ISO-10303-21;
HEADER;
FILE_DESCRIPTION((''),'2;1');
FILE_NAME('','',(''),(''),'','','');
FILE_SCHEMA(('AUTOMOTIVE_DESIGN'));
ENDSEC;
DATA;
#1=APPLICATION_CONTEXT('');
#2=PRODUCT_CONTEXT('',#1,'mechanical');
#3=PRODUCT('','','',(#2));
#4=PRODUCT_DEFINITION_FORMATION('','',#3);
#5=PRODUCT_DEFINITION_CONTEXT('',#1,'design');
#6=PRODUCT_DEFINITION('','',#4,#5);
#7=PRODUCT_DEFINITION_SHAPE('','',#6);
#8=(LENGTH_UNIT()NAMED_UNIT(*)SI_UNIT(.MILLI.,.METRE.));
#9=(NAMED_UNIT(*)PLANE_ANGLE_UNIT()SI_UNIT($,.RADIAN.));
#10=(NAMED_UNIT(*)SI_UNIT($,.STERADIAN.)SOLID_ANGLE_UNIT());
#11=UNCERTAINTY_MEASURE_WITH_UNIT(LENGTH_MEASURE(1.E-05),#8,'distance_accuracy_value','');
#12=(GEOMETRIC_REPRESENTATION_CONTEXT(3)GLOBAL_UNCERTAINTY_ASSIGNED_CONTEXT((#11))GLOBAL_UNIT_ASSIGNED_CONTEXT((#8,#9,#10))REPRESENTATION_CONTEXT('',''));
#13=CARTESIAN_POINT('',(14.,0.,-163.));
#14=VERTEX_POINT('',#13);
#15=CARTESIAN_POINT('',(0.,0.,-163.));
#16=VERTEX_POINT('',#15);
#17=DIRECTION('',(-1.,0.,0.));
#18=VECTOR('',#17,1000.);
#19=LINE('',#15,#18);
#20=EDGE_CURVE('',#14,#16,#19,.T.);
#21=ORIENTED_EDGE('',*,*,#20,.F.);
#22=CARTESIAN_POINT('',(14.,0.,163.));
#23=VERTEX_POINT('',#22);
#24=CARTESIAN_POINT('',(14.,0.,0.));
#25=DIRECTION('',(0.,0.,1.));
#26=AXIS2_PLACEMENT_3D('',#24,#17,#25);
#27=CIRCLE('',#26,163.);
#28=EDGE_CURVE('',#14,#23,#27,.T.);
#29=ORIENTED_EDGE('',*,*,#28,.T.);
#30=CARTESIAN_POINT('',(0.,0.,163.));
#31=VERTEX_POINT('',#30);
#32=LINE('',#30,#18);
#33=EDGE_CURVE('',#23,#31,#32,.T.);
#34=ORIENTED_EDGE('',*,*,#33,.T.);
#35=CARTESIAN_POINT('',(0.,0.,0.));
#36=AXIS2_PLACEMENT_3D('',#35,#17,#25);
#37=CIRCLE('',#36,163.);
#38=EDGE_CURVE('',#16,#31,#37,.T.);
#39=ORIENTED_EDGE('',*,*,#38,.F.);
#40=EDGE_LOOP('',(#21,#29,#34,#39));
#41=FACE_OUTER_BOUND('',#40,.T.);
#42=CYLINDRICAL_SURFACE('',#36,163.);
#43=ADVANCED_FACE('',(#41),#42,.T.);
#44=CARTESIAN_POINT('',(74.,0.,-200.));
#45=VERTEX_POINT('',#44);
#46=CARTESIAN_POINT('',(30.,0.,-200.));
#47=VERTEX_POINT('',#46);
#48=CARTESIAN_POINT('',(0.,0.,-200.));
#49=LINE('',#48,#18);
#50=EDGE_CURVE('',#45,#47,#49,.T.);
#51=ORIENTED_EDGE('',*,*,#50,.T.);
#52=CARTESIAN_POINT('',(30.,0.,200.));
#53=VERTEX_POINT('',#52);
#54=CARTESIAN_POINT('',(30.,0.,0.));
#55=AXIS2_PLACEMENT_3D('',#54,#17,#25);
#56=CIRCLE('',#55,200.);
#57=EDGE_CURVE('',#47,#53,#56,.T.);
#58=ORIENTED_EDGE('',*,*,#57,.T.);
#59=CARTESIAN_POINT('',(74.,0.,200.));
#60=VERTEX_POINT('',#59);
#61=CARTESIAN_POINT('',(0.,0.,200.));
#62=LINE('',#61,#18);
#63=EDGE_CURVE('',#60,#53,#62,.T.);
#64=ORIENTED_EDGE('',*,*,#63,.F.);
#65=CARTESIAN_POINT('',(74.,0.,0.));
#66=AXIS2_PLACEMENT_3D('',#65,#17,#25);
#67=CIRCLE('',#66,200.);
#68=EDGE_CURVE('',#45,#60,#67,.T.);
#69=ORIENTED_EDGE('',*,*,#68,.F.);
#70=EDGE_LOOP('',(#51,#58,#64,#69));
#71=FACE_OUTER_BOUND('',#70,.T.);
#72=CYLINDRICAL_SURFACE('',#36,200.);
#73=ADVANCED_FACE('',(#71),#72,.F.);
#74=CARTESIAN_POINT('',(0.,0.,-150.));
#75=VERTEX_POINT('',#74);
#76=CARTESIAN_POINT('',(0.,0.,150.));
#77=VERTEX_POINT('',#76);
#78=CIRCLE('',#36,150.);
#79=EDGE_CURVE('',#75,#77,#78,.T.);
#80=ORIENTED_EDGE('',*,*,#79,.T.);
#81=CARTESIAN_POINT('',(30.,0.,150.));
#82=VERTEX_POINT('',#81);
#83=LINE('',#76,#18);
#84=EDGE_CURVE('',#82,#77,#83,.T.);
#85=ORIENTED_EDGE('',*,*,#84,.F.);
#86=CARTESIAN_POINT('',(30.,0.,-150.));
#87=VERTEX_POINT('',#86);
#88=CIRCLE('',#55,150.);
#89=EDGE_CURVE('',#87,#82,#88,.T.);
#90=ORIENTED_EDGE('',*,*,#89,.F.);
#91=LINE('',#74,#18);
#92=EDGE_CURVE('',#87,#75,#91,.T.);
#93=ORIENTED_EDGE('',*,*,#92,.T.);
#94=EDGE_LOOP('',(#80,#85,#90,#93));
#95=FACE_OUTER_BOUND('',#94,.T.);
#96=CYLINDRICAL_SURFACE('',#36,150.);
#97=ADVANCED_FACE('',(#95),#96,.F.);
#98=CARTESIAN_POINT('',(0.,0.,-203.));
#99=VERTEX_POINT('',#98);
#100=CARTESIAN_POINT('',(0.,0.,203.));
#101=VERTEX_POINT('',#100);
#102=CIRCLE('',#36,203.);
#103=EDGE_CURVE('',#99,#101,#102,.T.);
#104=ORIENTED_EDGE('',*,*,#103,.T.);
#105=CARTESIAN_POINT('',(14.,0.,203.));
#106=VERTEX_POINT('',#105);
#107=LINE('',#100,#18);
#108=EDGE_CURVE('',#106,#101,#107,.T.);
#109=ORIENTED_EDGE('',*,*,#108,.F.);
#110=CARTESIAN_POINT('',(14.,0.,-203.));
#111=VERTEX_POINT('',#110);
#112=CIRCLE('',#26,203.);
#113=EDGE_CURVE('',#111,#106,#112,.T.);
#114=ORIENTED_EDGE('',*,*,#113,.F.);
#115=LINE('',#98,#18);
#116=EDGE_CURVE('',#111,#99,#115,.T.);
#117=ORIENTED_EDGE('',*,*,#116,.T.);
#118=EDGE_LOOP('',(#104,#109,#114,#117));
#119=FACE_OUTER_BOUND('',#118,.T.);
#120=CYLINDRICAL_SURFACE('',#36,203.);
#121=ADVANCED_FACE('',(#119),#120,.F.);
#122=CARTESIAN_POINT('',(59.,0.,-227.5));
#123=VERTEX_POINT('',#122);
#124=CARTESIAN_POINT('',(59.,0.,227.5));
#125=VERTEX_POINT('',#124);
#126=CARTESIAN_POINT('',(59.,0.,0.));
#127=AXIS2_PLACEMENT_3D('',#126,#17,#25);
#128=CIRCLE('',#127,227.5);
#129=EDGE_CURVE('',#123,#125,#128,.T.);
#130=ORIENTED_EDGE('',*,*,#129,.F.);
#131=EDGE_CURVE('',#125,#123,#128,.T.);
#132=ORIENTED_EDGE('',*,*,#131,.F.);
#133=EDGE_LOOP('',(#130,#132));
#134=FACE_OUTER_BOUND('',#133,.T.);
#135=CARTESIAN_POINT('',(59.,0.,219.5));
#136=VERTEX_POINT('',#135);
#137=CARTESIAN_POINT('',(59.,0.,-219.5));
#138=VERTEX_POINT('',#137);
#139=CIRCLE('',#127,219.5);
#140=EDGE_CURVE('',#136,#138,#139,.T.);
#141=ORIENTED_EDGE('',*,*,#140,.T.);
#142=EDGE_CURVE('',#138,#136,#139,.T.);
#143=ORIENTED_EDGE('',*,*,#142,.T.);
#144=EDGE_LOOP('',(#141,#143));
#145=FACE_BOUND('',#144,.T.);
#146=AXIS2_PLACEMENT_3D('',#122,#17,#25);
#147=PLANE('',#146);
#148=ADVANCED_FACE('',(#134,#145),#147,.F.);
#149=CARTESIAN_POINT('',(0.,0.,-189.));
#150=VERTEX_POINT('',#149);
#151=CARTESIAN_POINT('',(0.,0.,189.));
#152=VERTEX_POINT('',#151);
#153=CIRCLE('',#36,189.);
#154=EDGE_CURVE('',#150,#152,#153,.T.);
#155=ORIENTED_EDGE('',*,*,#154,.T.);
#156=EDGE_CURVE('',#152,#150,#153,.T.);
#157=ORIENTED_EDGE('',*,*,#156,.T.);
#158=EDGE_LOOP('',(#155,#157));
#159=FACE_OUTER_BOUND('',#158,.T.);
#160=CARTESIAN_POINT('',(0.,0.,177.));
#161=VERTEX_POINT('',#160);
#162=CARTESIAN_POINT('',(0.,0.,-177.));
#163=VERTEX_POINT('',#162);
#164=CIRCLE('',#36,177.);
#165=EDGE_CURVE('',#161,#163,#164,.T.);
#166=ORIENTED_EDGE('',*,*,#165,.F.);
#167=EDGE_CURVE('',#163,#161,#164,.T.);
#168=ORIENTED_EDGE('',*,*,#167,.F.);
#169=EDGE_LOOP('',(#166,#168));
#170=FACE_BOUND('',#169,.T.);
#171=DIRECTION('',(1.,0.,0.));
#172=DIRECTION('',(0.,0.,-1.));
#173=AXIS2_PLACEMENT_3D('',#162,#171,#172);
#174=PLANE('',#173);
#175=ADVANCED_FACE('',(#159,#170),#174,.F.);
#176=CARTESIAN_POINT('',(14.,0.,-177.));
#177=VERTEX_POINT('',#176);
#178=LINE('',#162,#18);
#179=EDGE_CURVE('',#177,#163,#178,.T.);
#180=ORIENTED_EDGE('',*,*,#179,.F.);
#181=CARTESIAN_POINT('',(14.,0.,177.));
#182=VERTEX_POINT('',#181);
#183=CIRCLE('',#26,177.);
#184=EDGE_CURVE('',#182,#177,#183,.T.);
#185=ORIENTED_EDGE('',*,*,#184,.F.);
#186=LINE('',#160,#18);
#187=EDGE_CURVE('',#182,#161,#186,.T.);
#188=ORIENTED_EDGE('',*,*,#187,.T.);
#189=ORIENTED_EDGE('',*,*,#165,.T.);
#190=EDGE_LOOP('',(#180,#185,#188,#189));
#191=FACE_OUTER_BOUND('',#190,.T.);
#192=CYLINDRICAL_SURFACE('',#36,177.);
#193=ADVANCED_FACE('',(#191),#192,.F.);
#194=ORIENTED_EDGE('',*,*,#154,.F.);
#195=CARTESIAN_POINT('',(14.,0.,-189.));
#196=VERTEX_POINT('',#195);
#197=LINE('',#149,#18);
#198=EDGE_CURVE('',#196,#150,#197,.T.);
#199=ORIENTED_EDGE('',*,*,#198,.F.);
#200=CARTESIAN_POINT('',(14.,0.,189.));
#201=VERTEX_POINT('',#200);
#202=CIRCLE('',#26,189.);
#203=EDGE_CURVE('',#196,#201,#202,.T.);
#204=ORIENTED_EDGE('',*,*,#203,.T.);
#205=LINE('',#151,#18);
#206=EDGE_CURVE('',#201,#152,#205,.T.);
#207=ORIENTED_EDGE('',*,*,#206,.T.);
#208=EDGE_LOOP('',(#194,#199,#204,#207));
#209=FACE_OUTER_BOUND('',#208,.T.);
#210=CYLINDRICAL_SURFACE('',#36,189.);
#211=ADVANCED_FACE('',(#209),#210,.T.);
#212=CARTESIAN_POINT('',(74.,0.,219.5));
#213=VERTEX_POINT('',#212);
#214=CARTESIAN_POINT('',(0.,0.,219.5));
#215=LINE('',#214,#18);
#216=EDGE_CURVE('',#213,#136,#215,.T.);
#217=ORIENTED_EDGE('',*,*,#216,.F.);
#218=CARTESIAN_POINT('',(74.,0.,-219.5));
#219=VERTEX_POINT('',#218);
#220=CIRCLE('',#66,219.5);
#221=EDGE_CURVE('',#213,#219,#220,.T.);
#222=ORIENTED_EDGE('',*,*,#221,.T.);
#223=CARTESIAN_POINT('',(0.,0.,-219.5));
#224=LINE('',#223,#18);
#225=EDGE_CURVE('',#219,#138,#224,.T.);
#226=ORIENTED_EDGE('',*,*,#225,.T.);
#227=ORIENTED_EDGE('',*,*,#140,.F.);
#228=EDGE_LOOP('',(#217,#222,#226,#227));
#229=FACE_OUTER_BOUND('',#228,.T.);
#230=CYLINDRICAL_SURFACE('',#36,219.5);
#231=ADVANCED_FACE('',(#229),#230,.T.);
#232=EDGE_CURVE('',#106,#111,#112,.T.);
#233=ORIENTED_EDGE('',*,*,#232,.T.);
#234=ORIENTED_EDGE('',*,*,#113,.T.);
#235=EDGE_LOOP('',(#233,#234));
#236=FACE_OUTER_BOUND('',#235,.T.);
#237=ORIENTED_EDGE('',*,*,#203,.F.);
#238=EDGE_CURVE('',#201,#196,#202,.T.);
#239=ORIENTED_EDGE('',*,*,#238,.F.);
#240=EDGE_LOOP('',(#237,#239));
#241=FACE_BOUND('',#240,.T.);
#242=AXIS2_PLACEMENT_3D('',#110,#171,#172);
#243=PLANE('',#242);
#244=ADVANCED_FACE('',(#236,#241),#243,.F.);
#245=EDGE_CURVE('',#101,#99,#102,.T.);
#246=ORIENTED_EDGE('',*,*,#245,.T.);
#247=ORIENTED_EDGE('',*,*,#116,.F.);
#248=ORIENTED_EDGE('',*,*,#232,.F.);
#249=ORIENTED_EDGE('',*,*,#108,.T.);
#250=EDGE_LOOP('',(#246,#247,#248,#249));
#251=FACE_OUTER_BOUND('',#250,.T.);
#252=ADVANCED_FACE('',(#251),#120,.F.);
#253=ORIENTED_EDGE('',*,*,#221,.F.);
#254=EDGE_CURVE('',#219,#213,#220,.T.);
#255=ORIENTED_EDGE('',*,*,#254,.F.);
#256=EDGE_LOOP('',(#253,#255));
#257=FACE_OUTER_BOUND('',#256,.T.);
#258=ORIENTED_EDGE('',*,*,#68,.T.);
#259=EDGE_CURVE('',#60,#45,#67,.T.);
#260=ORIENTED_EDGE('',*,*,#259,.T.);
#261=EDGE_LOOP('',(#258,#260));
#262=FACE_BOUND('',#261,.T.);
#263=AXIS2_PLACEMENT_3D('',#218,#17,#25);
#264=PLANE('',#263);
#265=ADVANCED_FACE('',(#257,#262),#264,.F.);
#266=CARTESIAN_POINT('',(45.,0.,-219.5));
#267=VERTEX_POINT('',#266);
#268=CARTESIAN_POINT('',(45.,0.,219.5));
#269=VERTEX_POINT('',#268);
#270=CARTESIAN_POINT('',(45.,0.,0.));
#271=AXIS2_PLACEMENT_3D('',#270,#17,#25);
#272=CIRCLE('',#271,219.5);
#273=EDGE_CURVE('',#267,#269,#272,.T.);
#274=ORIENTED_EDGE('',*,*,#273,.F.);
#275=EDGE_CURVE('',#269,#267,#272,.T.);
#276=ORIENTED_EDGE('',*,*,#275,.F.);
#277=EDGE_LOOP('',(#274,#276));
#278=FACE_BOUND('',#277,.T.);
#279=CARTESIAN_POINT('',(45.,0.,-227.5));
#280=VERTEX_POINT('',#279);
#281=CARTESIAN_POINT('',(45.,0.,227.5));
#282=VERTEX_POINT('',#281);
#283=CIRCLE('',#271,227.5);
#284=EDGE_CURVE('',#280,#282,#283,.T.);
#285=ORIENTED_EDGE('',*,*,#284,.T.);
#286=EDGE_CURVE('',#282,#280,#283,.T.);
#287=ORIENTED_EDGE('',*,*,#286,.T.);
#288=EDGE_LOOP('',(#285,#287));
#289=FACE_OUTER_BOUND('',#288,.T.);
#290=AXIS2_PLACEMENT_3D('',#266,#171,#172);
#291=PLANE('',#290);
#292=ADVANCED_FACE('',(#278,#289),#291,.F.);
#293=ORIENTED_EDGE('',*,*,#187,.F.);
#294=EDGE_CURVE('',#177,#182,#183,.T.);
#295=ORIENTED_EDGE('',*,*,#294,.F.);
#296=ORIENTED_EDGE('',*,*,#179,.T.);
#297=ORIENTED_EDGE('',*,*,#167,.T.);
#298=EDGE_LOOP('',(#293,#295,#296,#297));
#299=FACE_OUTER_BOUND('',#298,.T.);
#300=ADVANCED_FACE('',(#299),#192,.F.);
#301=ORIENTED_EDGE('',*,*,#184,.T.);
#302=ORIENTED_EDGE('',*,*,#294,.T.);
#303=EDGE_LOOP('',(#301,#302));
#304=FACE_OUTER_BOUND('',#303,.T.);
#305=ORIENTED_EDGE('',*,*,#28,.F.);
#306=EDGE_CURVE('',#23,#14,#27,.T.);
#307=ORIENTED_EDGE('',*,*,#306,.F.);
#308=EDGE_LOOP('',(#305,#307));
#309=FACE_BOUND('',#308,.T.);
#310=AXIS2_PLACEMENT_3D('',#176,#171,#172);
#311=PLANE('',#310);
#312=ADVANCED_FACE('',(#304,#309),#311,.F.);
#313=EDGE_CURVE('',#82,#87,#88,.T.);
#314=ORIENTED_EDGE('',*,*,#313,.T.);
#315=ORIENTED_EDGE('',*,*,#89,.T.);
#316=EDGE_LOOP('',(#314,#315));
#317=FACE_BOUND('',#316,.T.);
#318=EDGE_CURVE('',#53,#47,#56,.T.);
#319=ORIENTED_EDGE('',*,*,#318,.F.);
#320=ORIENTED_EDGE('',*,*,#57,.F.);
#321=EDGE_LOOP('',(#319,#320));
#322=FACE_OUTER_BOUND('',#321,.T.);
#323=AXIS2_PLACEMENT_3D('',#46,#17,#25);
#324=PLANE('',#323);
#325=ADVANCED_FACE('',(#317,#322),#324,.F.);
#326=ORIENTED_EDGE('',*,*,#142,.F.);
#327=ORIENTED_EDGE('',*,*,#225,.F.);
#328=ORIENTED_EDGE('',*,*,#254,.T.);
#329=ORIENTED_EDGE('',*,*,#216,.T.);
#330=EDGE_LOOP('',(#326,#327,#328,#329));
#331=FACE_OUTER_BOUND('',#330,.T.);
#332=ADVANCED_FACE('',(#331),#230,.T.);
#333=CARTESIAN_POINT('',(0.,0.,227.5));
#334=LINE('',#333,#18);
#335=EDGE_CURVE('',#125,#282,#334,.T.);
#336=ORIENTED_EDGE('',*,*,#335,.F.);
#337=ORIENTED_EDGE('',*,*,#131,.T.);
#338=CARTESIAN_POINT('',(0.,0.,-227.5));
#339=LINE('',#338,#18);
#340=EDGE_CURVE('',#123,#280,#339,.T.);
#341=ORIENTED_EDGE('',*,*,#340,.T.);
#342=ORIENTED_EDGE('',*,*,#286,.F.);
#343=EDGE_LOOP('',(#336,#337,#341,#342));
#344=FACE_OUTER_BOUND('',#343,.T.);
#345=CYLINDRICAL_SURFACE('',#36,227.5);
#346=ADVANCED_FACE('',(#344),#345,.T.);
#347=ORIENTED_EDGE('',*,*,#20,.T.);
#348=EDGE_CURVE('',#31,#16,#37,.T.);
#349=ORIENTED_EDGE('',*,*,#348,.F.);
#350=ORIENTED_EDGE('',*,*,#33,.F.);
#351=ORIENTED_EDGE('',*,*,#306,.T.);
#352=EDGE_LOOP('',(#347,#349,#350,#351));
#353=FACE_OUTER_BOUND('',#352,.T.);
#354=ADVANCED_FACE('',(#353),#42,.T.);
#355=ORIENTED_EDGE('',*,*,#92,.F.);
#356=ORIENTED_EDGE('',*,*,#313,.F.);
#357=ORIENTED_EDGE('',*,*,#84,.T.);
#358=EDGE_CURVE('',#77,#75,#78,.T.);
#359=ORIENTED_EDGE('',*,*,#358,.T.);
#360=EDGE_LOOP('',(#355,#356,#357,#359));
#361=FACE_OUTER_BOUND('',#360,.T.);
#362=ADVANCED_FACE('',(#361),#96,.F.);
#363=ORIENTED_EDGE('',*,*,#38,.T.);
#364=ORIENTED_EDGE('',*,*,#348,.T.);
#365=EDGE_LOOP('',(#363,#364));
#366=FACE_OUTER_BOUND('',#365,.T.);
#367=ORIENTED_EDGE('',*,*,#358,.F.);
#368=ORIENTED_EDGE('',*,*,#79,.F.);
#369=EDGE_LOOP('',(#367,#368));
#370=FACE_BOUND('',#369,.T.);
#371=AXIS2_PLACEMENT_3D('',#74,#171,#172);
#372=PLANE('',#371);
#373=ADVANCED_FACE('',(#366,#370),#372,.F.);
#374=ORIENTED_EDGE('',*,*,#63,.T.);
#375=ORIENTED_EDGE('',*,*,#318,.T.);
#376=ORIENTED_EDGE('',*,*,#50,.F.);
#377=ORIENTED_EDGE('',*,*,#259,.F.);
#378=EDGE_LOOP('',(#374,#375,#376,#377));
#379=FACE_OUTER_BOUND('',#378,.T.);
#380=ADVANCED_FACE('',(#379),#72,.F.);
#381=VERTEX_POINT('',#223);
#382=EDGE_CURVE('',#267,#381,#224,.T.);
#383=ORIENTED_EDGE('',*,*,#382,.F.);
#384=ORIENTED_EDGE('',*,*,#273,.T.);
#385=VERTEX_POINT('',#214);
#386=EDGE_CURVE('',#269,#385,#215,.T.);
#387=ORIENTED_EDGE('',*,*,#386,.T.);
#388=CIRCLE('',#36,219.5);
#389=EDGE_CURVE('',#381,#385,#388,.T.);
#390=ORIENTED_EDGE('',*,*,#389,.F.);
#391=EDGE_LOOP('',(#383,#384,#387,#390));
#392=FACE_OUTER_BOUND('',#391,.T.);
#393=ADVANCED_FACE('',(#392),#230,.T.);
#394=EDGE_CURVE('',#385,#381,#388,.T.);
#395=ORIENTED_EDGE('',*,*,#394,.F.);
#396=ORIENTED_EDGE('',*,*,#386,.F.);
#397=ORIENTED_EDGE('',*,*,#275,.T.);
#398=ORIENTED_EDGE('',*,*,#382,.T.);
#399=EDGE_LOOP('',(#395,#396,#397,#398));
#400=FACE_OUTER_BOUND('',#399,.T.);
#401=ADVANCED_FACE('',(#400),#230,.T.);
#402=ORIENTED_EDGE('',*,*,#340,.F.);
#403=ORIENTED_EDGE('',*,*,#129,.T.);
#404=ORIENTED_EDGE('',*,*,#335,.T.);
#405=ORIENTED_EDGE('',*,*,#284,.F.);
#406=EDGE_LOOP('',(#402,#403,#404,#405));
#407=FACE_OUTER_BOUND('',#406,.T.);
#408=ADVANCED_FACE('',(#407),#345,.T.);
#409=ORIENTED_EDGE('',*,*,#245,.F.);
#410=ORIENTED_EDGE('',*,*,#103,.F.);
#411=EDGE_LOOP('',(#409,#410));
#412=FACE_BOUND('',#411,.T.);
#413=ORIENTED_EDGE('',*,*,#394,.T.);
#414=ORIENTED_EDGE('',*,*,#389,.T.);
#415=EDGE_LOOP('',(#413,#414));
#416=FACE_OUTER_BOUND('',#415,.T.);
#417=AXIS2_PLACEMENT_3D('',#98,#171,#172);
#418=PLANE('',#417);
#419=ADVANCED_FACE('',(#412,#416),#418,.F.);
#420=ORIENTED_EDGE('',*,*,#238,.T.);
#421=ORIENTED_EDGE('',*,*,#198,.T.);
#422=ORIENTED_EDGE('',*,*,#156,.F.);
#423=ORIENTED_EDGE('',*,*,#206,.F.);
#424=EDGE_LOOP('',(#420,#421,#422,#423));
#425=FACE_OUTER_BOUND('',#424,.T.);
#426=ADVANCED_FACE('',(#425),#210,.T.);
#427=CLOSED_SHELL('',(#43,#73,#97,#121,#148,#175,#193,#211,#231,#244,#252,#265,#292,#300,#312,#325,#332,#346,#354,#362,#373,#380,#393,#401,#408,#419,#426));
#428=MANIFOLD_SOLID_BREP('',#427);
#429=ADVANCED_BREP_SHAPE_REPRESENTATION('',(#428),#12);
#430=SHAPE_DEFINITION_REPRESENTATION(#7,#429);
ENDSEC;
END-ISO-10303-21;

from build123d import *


with BuildPart() as part:
    # Sketch1 → Revolve1 (revolve)
    with BuildSketch(Plane(origin=(0, 0, 0), x_dir=(1, 0, 0), z_dir=(0, 1, 0)), mode=Mode.PRIVATE) as revolve1_sk:
        Polygon((0, 150), (0, 163), (14, 163), (14, 177), (0, 177), (0, 189), (14, 189), (14, 203), (0, 203), (0, 219.5), (45, 219.5), (45, 227.5), (59, 227.5), (59, 219.5), (74, 219.5), (74, 200), (30, 200), (30, 150), align=None)
    revolve(revolve1_sk.sketch.rotate(Axis((0, 0, 0), (1, 0, 0)), 180), axis=Axis((0, 0, 0), (1, 0, 0)))


solid = part.part
